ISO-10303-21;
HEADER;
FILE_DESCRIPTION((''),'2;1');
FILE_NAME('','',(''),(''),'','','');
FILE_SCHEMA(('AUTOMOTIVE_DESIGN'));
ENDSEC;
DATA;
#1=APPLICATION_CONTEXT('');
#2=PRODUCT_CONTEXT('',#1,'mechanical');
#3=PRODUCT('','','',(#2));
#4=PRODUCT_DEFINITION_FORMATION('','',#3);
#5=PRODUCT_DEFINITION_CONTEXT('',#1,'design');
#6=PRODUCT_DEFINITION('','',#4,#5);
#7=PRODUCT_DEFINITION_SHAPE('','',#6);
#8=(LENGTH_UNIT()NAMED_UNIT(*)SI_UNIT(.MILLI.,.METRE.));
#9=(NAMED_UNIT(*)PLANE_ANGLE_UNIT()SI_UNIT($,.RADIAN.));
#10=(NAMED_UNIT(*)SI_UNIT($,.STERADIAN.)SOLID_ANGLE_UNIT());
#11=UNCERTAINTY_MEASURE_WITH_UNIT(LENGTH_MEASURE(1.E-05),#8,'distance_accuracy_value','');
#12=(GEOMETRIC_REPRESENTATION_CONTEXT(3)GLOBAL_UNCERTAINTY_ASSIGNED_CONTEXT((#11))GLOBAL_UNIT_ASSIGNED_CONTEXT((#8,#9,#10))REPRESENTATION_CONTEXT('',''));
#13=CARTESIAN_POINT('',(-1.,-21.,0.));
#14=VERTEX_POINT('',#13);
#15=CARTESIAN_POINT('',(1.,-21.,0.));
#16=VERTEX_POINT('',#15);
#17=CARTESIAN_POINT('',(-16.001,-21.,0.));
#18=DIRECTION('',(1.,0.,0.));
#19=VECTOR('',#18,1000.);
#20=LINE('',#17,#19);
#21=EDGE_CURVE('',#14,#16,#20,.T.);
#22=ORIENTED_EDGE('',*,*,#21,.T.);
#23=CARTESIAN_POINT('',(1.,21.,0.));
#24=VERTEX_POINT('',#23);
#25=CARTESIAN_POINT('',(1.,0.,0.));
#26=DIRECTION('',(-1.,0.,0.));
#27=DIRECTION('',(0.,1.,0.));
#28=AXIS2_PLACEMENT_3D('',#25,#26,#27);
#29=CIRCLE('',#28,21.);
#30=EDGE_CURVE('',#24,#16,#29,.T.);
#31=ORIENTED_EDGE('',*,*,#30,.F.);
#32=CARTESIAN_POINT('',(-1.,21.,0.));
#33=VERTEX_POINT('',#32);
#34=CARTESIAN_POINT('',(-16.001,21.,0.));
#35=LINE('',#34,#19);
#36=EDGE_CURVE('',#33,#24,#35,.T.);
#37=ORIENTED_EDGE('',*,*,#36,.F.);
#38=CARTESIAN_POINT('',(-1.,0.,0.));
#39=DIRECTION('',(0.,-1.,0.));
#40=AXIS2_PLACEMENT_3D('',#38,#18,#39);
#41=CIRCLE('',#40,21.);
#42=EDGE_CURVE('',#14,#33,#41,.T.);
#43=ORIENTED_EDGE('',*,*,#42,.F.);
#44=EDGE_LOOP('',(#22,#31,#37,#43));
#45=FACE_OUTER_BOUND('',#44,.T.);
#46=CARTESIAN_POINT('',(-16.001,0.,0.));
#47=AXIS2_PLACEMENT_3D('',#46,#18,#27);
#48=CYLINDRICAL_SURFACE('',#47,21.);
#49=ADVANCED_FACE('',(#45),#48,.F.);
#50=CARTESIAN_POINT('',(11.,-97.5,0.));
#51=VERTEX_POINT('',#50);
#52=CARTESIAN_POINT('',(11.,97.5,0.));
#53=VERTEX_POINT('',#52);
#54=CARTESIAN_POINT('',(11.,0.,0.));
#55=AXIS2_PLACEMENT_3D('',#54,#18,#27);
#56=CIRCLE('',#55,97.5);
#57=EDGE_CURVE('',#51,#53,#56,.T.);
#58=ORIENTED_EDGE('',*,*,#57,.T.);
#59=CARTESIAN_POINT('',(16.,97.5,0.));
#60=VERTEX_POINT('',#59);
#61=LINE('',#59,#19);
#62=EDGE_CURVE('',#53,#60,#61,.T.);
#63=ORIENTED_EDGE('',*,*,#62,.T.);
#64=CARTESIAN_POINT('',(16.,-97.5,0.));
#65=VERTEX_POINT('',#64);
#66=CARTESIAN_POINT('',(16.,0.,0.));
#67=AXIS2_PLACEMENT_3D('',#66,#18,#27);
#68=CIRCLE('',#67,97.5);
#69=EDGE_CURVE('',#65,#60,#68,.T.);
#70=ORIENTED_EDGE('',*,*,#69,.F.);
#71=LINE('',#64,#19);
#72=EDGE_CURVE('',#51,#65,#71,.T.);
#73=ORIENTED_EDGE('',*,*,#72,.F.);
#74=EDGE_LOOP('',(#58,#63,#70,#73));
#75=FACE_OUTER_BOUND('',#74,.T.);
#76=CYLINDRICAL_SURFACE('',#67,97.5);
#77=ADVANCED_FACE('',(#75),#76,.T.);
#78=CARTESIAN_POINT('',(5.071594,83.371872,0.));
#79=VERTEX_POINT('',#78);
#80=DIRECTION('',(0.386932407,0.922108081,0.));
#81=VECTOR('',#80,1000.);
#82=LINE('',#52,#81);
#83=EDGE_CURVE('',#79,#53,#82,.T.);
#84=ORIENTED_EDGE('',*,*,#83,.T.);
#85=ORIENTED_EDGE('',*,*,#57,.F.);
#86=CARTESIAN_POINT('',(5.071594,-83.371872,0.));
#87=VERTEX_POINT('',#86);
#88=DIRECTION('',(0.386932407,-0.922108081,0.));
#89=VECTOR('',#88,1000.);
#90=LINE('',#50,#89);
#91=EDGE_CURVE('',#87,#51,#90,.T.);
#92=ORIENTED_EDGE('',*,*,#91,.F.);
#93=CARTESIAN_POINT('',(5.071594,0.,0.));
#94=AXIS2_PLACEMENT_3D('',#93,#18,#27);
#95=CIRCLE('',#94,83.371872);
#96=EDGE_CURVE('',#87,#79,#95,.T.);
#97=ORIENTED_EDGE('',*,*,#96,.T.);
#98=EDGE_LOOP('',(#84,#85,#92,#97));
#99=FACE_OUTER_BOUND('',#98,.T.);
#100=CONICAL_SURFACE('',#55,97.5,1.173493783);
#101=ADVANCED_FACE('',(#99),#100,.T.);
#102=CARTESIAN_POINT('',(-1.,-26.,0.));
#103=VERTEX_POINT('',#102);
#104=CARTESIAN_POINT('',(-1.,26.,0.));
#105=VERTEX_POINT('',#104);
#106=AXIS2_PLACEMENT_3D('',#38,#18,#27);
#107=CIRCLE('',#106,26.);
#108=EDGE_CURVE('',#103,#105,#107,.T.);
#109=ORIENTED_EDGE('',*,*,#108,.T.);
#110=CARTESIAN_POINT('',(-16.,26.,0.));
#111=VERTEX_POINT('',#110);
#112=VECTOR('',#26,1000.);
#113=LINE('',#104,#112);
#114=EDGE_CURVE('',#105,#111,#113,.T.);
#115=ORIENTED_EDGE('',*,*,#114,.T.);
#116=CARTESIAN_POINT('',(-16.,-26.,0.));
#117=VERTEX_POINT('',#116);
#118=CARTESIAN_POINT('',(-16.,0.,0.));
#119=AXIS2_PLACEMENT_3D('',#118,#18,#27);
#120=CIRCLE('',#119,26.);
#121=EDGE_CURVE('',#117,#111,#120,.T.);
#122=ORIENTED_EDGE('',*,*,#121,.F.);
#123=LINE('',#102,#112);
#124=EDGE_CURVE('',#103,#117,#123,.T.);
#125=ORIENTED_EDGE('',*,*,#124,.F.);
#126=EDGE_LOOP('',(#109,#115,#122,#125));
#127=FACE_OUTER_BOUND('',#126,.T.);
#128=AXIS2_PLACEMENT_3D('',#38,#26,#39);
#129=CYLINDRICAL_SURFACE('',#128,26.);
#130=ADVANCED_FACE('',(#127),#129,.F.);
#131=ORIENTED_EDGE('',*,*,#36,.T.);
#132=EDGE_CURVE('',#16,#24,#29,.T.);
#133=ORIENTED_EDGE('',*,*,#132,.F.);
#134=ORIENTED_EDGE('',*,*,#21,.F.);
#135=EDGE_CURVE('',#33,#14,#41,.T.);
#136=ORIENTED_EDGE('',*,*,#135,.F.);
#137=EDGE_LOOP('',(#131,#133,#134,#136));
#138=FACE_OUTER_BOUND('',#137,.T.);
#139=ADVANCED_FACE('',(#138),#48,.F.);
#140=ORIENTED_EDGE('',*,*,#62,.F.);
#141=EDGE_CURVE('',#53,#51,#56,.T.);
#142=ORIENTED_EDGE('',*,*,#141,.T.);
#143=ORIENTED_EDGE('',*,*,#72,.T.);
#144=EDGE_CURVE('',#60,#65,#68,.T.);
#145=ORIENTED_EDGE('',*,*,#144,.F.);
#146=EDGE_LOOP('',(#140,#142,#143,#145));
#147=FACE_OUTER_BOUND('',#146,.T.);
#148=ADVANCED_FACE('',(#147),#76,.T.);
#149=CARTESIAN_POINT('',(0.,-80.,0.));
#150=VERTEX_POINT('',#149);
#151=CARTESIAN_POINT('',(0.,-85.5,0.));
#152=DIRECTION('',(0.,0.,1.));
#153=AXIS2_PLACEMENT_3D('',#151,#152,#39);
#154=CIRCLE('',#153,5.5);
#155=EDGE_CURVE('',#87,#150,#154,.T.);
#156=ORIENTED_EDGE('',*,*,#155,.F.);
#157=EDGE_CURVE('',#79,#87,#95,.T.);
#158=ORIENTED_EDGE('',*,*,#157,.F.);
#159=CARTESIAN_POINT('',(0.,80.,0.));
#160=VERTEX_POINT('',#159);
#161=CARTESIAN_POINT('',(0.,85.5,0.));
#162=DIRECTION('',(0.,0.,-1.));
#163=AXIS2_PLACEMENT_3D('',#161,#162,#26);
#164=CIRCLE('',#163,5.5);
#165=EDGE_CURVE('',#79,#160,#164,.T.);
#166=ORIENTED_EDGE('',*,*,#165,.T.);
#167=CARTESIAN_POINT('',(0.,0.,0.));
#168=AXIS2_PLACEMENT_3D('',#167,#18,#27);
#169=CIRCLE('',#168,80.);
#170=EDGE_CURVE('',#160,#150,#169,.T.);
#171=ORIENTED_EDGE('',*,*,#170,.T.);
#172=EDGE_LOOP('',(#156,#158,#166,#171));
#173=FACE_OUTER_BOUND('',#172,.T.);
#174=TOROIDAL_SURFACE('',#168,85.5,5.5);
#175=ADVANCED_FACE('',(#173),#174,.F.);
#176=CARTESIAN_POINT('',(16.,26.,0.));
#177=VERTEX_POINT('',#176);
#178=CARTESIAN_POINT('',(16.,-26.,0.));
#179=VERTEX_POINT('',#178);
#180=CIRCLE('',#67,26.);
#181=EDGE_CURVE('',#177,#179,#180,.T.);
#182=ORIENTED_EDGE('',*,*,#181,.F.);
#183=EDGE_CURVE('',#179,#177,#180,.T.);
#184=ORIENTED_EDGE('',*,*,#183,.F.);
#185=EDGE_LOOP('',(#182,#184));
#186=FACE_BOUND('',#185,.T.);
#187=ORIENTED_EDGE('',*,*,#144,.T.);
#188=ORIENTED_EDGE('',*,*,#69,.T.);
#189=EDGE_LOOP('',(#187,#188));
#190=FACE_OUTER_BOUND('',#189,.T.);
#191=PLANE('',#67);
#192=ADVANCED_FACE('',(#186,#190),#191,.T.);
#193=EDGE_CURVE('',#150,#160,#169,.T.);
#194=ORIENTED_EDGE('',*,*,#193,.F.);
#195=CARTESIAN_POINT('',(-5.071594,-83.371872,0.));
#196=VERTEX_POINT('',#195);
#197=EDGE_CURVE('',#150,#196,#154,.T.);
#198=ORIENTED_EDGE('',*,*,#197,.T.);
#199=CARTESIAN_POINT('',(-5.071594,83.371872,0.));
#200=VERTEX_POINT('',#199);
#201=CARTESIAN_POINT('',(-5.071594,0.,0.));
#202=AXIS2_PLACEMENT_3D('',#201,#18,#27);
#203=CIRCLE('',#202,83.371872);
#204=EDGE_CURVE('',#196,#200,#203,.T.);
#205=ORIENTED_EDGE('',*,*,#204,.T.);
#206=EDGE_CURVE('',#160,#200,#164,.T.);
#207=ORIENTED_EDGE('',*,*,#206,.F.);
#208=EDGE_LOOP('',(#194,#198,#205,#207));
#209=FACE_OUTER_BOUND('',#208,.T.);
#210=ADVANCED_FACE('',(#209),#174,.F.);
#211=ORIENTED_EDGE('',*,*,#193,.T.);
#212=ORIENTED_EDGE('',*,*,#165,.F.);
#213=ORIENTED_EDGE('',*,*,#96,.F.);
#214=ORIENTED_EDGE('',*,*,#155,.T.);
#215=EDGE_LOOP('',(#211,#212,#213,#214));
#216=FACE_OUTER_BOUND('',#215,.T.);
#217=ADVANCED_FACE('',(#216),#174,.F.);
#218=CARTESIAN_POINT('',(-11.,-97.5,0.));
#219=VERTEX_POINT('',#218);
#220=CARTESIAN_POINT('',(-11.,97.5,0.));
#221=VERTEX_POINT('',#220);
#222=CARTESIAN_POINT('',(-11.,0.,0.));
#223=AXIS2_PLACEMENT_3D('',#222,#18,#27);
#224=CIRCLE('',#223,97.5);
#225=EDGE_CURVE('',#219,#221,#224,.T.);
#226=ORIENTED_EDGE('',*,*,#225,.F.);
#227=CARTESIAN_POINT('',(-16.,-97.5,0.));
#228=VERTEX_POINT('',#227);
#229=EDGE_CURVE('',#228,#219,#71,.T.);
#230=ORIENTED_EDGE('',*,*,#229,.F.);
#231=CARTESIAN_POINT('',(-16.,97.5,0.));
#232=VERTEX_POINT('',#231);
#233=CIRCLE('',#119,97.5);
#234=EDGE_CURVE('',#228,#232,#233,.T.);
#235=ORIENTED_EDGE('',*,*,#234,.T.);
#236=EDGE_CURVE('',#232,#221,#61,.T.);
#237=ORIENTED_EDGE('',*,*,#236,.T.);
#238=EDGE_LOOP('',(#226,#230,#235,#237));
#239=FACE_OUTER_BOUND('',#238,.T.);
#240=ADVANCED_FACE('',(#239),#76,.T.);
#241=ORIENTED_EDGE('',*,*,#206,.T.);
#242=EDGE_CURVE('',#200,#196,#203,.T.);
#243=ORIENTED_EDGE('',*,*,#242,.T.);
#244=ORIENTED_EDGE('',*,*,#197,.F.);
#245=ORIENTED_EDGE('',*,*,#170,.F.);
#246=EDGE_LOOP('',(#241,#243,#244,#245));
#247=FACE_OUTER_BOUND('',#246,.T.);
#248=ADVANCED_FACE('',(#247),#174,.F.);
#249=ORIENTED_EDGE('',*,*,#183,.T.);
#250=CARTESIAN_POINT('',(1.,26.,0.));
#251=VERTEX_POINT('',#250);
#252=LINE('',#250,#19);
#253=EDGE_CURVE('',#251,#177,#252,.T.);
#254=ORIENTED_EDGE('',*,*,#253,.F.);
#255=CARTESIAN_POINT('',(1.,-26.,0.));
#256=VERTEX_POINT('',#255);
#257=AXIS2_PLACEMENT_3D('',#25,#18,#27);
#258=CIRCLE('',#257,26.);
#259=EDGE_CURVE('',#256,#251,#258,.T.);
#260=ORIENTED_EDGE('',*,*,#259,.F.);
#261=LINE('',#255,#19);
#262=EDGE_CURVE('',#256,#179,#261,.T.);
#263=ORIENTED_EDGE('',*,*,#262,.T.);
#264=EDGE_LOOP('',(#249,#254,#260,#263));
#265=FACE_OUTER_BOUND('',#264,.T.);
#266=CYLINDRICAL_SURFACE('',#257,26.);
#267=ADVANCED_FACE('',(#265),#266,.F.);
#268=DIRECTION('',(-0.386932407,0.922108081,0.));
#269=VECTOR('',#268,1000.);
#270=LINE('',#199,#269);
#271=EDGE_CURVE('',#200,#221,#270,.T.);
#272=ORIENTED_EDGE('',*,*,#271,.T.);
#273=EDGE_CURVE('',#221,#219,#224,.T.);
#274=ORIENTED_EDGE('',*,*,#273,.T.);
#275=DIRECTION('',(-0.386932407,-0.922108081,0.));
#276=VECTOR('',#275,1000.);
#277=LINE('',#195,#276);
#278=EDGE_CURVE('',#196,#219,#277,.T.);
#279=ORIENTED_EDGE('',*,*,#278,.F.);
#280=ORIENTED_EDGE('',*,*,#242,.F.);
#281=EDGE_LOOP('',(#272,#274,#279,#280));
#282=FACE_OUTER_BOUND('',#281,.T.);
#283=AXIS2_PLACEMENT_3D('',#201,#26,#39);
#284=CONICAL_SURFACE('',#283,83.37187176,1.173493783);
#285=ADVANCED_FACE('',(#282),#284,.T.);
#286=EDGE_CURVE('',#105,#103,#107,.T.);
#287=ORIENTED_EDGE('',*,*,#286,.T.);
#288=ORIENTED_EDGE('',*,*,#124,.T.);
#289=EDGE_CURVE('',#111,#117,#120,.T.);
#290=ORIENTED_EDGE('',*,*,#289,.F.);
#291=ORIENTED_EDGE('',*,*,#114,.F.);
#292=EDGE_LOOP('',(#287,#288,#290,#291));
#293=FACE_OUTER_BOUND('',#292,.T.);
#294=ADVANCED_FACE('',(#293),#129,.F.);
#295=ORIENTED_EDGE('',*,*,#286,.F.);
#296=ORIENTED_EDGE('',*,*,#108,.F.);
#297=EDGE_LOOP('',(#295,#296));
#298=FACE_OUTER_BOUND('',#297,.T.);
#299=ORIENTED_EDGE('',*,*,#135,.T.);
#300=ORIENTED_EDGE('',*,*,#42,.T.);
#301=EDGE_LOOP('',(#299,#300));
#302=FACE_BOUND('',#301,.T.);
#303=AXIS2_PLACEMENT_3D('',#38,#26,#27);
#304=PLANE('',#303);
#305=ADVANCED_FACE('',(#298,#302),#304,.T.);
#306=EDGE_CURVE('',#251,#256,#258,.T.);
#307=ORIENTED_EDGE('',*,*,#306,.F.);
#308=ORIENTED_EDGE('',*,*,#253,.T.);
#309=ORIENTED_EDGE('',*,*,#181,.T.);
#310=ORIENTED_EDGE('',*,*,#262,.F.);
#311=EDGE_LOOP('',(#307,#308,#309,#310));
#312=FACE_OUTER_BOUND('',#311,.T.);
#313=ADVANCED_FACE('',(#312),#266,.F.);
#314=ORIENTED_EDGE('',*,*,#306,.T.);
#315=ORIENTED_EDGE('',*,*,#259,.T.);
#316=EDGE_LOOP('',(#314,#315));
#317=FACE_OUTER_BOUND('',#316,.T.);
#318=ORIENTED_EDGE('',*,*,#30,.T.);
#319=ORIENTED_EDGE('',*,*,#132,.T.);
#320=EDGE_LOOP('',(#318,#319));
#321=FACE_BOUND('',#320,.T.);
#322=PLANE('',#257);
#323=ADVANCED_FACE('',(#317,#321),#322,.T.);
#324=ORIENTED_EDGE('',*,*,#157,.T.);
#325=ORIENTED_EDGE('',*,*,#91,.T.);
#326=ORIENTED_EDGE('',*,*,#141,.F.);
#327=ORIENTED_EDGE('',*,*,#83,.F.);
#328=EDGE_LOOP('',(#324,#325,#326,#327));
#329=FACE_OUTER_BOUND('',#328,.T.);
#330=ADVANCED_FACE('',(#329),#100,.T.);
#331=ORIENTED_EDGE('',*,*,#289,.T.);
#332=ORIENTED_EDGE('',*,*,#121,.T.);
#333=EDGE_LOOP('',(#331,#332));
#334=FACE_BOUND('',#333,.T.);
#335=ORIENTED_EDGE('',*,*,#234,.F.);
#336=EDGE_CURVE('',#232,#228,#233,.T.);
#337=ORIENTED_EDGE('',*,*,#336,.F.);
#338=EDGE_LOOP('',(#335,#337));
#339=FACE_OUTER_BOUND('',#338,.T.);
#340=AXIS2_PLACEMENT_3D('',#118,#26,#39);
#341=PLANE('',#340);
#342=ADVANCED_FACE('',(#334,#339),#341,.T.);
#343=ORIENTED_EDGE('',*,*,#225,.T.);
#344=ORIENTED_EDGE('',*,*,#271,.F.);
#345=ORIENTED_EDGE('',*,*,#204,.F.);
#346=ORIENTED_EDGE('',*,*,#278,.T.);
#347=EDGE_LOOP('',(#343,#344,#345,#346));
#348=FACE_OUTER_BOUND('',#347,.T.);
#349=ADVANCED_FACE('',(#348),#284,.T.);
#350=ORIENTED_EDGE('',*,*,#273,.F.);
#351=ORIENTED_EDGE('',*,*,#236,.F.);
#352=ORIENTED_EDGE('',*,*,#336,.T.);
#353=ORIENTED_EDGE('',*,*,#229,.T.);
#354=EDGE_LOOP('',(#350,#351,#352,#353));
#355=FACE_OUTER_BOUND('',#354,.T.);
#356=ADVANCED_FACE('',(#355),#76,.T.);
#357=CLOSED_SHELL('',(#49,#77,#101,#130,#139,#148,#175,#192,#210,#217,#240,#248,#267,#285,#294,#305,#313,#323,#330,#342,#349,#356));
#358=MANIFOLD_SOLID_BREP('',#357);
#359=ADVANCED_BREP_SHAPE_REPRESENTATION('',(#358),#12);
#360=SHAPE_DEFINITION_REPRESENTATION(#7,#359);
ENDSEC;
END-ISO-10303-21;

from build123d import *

# Parameters (mm, degrees)
CUT_EXTRUDE1_REACH = 143.55
SKETCH2_R          = 21
SKETCH3_R          = 26
CUT_EXTRUDE2_DEPTH = 15


with BuildPart() as part:
    # Sketch1 → Revolve1 (revolve)
    with BuildSketch(Plane.XY):
        with BuildLine():
            Line((-16, 0), (-16, 97.5))
            Line((-16, 97.5), (-11, 97.5))
            Line((-11, 97.5), (-5.071594443, 83.37187176))
            ThreePointArc((-5.071594443, 83.37187176), (0, 80), (5.071594443, 83.37187176))
            Line((5.071594443, 83.37187176), (11, 97.5))
            Line((11, 97.5), (16, 97.5))
            Line((16, 97.5), (16, 0))
            Line((16, 0), (-16, 0))
        make_face()
    revolve(axis=Axis((16, 0, 0), (-1, 0, 0)))

    # Sketch2 → Cut-Extrude1 (cut, up to next)
    with BuildSketch(Plane(origin=(16, 0, 0), x_dir=(0, 0, -1), z_dir=(1, 0, 0)), mode=Mode.PRIVATE) as cut_extrude1_sk1:
        with Locations(Location((0, 0, 0), (0, 0, 90))):
            Circle(SKETCH2_R)
    cut_extrude1_tool1 = extrude(cut_extrude1_sk1.sketch, amount=-CUT_EXTRUDE1_REACH, mode=Mode.PRIVATE) & part.part
    add(cut_extrude1_tool1.solids().sort_by_distance((16, 0, 0))[0], mode=Mode.SUBTRACT)

    # Sketch3 → Cut-Extrude2 (cut)
    with BuildSketch(Plane(origin=(16, 0, 0), x_dir=(0, 0, -1), z_dir=(1, 0, 0))):
        with Locations(Location((0, 0, 0), (0, 0, 90))):
            Circle(SKETCH3_R)
    cut_extrude2 = extrude(amount=-CUT_EXTRUDE2_DEPTH, mode=Mode.SUBTRACT)

    # Mirror1: Cut-Extrude2 across plane
    add(cut_extrude2.mirror(Plane(origin=(0, 0, 0), x_dir=(0, 0, 1), z_dir=(1, 0, 0))), mode=Mode.SUBTRACT)


solid = part.part
